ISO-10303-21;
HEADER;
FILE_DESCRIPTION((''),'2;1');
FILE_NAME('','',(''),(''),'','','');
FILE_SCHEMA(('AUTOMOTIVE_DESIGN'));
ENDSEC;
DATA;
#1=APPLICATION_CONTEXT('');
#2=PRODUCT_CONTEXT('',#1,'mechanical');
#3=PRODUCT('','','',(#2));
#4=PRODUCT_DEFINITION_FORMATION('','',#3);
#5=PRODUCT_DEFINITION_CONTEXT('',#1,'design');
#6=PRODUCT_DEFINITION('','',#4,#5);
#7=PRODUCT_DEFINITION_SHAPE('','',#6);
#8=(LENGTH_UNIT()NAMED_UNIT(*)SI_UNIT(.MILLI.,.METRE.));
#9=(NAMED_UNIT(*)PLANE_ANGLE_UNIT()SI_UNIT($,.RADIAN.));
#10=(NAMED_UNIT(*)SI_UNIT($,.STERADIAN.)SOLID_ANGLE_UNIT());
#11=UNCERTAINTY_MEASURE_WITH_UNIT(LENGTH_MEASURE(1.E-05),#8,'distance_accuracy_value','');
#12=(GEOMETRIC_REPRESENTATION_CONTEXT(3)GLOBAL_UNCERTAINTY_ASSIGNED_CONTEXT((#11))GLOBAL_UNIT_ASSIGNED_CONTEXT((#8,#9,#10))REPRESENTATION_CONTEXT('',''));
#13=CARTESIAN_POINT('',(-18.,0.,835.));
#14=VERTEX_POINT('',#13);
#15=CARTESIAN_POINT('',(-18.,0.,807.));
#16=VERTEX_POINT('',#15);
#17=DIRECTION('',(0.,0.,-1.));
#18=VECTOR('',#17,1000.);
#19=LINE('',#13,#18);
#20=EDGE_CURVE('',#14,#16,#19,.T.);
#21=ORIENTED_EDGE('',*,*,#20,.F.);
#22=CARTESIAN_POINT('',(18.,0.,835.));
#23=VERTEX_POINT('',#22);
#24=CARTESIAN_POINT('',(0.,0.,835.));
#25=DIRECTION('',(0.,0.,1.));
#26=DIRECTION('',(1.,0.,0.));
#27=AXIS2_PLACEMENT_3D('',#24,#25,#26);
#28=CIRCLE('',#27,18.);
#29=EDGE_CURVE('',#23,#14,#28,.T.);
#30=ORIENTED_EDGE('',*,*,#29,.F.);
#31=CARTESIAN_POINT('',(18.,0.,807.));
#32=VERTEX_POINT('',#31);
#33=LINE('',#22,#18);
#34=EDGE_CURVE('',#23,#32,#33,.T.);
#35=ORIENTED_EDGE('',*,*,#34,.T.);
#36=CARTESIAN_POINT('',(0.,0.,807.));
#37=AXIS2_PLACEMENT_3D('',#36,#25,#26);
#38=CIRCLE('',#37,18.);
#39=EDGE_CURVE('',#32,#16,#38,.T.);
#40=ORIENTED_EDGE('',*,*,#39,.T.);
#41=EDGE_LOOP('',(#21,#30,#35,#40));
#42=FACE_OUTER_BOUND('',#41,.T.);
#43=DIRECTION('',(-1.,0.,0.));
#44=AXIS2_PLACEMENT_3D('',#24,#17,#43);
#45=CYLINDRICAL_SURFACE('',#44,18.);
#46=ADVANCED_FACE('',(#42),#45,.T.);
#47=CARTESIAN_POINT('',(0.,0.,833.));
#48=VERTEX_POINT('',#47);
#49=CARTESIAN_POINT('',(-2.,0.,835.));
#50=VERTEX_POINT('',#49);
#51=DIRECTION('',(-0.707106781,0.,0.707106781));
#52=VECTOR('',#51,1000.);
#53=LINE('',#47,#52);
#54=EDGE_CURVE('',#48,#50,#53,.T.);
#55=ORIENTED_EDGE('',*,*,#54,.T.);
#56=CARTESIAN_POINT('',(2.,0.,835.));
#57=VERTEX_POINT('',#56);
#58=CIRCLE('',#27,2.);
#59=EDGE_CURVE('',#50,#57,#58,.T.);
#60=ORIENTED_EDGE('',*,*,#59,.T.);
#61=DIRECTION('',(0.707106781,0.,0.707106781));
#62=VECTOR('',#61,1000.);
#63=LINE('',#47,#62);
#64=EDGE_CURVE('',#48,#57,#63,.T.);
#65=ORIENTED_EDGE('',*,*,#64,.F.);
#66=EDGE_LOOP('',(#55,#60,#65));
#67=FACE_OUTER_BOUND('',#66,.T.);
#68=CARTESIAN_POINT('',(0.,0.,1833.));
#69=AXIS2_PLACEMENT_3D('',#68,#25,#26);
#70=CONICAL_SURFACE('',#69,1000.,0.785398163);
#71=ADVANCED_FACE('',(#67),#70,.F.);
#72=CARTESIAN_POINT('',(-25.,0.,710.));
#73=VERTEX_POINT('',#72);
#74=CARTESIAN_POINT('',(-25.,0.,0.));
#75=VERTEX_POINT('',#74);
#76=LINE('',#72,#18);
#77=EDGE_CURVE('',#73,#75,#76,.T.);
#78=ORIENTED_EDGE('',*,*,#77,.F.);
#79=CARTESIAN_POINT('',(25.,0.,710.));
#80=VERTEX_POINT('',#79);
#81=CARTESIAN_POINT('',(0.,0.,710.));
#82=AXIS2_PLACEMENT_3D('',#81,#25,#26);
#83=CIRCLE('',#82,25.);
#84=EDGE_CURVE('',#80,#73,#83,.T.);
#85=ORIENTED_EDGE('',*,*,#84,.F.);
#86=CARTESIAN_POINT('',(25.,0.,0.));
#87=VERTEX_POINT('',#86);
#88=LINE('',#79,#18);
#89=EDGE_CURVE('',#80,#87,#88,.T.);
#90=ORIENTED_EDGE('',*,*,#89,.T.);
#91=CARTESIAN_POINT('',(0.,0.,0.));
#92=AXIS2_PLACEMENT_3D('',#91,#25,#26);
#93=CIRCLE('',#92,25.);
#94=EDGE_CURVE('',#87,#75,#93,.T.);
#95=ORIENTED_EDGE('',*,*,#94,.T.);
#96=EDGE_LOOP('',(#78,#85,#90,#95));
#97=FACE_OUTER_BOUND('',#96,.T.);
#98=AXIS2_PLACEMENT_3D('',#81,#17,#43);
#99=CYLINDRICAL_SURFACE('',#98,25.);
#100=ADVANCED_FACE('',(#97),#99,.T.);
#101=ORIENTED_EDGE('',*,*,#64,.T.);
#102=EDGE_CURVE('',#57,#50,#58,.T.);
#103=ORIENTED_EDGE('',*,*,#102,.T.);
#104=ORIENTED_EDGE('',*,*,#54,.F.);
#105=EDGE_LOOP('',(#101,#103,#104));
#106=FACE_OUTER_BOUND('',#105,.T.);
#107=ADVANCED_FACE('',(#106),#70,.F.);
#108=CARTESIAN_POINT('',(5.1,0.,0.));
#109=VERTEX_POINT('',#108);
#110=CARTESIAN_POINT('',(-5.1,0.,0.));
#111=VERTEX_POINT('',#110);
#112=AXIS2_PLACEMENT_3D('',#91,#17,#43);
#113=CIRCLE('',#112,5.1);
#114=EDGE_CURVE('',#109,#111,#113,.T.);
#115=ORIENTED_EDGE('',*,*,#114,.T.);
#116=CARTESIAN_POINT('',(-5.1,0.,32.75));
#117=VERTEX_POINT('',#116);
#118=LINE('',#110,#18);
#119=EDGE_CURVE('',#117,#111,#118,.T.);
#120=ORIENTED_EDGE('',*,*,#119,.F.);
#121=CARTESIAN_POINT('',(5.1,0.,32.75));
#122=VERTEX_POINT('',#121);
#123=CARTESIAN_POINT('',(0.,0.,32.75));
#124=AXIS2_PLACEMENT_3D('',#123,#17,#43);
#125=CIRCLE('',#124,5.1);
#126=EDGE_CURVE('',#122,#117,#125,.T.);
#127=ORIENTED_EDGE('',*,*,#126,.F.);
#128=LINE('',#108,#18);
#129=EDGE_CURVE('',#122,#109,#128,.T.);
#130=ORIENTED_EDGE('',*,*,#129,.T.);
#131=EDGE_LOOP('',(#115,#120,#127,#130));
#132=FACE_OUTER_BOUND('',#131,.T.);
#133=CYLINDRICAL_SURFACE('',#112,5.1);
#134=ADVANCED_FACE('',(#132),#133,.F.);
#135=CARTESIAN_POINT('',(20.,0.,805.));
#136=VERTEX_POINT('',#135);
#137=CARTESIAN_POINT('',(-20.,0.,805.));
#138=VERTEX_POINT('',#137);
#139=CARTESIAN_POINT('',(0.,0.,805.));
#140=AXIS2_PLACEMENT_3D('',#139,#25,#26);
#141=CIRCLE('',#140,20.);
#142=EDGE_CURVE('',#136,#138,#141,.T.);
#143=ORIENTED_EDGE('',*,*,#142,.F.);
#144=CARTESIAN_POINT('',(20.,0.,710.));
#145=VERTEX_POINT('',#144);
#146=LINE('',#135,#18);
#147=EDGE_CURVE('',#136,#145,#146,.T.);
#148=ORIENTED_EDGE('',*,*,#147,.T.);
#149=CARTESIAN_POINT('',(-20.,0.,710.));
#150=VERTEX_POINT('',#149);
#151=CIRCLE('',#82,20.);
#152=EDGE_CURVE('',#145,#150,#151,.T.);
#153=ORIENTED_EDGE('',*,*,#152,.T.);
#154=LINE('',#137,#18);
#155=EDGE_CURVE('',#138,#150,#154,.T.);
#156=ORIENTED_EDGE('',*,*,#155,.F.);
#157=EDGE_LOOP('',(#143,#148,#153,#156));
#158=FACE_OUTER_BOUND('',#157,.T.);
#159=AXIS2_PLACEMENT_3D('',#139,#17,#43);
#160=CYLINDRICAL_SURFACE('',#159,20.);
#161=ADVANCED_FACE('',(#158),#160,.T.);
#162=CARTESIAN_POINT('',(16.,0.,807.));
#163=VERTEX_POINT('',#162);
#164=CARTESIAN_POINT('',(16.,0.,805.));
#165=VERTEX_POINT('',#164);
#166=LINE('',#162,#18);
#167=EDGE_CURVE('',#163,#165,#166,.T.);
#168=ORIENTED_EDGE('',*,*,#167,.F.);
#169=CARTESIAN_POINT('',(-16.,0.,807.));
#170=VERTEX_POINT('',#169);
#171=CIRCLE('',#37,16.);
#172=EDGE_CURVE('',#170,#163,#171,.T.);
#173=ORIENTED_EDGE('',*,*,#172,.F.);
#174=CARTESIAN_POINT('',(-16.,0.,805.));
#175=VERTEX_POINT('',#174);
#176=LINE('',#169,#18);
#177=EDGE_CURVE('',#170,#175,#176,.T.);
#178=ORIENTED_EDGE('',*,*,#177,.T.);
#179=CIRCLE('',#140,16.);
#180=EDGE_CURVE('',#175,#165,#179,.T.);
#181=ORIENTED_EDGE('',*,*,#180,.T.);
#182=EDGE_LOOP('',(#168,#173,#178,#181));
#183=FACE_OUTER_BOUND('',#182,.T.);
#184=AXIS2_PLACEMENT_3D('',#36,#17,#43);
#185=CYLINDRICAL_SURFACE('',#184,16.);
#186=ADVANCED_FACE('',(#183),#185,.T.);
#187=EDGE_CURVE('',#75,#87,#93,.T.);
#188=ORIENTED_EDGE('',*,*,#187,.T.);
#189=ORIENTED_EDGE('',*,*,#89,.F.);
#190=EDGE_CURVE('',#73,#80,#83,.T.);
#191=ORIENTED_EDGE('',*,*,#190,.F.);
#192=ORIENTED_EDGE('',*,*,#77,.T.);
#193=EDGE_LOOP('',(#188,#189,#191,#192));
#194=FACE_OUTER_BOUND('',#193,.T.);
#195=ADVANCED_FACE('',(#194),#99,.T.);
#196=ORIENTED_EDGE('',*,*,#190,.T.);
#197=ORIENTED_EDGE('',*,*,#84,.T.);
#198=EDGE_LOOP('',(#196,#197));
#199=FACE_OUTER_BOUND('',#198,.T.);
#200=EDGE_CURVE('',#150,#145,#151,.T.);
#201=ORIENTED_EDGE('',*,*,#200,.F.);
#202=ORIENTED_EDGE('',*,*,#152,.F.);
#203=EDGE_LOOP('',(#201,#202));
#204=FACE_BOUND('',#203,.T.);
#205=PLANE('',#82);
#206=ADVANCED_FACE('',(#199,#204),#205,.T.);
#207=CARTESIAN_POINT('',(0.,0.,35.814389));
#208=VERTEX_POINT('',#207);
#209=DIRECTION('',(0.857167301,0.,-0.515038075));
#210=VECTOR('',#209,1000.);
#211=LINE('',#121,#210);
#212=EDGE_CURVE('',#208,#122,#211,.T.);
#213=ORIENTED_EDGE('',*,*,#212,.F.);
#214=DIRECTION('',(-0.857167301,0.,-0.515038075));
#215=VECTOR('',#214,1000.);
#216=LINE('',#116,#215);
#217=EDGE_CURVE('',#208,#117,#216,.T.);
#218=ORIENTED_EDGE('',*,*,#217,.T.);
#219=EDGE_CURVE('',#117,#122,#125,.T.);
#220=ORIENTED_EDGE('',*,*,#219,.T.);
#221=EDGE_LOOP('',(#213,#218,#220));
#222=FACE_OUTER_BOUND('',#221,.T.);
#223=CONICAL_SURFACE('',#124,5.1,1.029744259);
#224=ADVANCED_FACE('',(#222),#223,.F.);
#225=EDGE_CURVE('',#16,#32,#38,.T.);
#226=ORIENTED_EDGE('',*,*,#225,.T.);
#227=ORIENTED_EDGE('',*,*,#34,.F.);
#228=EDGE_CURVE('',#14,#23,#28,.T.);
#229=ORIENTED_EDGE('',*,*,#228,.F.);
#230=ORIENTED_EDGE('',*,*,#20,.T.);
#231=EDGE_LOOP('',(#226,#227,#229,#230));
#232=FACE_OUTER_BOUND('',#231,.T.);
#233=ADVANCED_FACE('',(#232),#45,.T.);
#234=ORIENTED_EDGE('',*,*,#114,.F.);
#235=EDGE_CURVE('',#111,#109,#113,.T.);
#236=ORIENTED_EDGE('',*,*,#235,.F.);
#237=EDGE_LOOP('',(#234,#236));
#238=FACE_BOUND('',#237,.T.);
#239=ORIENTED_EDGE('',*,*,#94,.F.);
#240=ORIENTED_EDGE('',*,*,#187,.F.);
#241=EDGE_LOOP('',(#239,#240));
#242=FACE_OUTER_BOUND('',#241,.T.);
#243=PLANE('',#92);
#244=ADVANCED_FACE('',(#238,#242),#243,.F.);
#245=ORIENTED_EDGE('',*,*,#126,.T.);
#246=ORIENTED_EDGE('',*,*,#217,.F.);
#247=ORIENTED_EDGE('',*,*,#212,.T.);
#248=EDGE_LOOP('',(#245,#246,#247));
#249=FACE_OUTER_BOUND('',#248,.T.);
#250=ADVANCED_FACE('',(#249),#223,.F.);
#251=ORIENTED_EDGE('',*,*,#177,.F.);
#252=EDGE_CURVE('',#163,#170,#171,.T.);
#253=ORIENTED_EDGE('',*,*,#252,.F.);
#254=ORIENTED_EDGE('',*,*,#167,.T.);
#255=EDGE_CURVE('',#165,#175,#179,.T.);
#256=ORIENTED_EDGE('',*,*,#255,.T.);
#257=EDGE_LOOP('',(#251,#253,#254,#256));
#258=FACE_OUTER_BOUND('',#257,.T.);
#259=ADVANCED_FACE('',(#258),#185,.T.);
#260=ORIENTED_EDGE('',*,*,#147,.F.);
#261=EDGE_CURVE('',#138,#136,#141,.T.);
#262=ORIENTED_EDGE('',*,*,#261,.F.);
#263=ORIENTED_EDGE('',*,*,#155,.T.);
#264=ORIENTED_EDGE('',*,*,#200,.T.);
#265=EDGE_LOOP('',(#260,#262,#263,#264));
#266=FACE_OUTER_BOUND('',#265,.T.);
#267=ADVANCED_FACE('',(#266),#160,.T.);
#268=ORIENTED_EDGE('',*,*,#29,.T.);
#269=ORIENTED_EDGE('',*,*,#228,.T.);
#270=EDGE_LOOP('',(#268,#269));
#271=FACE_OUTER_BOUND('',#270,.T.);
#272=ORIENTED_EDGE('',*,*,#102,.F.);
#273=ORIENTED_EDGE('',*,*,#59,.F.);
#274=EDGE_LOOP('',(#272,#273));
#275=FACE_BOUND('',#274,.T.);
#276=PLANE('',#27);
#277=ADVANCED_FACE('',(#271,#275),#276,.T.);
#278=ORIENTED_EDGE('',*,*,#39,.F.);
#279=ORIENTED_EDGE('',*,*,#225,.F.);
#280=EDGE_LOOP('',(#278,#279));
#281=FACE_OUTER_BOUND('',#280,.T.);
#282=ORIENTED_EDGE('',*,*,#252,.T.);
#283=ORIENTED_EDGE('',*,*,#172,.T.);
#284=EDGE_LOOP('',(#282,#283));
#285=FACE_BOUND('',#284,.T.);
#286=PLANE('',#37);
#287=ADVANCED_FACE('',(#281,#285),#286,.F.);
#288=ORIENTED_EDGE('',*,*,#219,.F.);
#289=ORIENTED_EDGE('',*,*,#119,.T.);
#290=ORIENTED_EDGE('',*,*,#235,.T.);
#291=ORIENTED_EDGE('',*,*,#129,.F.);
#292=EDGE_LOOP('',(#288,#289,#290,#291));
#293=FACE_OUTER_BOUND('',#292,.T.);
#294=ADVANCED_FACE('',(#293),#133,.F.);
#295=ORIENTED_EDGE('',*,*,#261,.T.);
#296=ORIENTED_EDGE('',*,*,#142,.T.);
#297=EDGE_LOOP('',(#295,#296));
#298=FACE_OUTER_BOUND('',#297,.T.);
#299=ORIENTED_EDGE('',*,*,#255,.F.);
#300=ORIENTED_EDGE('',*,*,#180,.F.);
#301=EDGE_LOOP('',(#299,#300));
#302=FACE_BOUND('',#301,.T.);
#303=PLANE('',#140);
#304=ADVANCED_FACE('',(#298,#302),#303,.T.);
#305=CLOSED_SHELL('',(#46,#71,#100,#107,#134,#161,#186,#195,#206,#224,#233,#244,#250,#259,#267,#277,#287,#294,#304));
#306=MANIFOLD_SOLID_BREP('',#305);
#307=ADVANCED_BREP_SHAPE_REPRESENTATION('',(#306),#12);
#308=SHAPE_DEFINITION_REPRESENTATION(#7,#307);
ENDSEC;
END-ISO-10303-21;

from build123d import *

# Parameters (mm, degrees)
SKETCH_1_R              = 25
EXTRUDE_1_DEPTH         = 710
SKETCH_2_R              = 20
EXTRUDE_2_DEPTH         = 95
SKETCH_3_R              = 18
EXTRUDE_3_DEPTH         = 30
HOLE_WIZARD_M12_1_D     = 10.2
HOLE_WIZARD_M12_1_DEPTH = 32.75
HOLE_WIZARD_M12_1_TIP   = 3.064389157
SKETCH_8_R              = 20
SKETCH_8_R_2            = 16
CUT_EXTRUDE_1_DEPTH     = 2


with BuildPart() as part:
    # 草图1 → 拉伸1 (new body)
    with BuildSketch(Plane.XY):
        Circle(SKETCH_1_R)
    extrude(amount=EXTRUDE_1_DEPTH)

    # 草图2 → 拉伸2 (add)
    with BuildSketch(Plane.XY.offset(710)):
        Circle(SKETCH_2_R)
    extrude(amount=EXTRUDE_2_DEPTH)

    # 草图3 → 拉伸3 (add)
    with BuildSketch(Plane.XY.offset(805)):
        Circle(SKETCH_3_R)
    extrude(amount=EXTRUDE_3_DEPTH)

    # M12 螺纹孔1
    with Locations(Plane(origin=(0, 0, 0), x_dir=(-1, 0, 0), z_dir=(0, 0, -1))):
        with Locations((0, 0)):
            Hole(HOLE_WIZARD_M12_1_D / 2, depth=HOLE_WIZARD_M12_1_DEPTH)
            with Locations((0, 0, -(HOLE_WIZARD_M12_1_DEPTH + HOLE_WIZARD_M12_1_TIP / 2))):  # 118° drill point
                Cone(0, HOLE_WIZARD_M12_1_D / 2, HOLE_WIZARD_M12_1_TIP, mode=Mode.SUBTRACT)

    # 草图7 → 切除-旋转1 (revolve, cut)
    with BuildSketch(Plane(origin=(0, 0, 0), x_dir=(1, 0, 0), z_dir=(0, 1, 0))):
        Polygon((-2, -835), (0, -833), (0, -835), align=None)
    revolve(axis=Axis((0, 0, 835), (0, 0, -1)), mode=Mode.SUBTRACT)

    # 草图8 → 切除-拉伸1 (cut)
    with BuildSketch(Plane.XY.offset(805)):
        Circle(SKETCH_8_R)
        Circle(SKETCH_8_R_2, mode=Mode.SUBTRACT)
    extrude(amount=CUT_EXTRUDE_1_DEPTH, mode=Mode.SUBTRACT)


solid = part.part
